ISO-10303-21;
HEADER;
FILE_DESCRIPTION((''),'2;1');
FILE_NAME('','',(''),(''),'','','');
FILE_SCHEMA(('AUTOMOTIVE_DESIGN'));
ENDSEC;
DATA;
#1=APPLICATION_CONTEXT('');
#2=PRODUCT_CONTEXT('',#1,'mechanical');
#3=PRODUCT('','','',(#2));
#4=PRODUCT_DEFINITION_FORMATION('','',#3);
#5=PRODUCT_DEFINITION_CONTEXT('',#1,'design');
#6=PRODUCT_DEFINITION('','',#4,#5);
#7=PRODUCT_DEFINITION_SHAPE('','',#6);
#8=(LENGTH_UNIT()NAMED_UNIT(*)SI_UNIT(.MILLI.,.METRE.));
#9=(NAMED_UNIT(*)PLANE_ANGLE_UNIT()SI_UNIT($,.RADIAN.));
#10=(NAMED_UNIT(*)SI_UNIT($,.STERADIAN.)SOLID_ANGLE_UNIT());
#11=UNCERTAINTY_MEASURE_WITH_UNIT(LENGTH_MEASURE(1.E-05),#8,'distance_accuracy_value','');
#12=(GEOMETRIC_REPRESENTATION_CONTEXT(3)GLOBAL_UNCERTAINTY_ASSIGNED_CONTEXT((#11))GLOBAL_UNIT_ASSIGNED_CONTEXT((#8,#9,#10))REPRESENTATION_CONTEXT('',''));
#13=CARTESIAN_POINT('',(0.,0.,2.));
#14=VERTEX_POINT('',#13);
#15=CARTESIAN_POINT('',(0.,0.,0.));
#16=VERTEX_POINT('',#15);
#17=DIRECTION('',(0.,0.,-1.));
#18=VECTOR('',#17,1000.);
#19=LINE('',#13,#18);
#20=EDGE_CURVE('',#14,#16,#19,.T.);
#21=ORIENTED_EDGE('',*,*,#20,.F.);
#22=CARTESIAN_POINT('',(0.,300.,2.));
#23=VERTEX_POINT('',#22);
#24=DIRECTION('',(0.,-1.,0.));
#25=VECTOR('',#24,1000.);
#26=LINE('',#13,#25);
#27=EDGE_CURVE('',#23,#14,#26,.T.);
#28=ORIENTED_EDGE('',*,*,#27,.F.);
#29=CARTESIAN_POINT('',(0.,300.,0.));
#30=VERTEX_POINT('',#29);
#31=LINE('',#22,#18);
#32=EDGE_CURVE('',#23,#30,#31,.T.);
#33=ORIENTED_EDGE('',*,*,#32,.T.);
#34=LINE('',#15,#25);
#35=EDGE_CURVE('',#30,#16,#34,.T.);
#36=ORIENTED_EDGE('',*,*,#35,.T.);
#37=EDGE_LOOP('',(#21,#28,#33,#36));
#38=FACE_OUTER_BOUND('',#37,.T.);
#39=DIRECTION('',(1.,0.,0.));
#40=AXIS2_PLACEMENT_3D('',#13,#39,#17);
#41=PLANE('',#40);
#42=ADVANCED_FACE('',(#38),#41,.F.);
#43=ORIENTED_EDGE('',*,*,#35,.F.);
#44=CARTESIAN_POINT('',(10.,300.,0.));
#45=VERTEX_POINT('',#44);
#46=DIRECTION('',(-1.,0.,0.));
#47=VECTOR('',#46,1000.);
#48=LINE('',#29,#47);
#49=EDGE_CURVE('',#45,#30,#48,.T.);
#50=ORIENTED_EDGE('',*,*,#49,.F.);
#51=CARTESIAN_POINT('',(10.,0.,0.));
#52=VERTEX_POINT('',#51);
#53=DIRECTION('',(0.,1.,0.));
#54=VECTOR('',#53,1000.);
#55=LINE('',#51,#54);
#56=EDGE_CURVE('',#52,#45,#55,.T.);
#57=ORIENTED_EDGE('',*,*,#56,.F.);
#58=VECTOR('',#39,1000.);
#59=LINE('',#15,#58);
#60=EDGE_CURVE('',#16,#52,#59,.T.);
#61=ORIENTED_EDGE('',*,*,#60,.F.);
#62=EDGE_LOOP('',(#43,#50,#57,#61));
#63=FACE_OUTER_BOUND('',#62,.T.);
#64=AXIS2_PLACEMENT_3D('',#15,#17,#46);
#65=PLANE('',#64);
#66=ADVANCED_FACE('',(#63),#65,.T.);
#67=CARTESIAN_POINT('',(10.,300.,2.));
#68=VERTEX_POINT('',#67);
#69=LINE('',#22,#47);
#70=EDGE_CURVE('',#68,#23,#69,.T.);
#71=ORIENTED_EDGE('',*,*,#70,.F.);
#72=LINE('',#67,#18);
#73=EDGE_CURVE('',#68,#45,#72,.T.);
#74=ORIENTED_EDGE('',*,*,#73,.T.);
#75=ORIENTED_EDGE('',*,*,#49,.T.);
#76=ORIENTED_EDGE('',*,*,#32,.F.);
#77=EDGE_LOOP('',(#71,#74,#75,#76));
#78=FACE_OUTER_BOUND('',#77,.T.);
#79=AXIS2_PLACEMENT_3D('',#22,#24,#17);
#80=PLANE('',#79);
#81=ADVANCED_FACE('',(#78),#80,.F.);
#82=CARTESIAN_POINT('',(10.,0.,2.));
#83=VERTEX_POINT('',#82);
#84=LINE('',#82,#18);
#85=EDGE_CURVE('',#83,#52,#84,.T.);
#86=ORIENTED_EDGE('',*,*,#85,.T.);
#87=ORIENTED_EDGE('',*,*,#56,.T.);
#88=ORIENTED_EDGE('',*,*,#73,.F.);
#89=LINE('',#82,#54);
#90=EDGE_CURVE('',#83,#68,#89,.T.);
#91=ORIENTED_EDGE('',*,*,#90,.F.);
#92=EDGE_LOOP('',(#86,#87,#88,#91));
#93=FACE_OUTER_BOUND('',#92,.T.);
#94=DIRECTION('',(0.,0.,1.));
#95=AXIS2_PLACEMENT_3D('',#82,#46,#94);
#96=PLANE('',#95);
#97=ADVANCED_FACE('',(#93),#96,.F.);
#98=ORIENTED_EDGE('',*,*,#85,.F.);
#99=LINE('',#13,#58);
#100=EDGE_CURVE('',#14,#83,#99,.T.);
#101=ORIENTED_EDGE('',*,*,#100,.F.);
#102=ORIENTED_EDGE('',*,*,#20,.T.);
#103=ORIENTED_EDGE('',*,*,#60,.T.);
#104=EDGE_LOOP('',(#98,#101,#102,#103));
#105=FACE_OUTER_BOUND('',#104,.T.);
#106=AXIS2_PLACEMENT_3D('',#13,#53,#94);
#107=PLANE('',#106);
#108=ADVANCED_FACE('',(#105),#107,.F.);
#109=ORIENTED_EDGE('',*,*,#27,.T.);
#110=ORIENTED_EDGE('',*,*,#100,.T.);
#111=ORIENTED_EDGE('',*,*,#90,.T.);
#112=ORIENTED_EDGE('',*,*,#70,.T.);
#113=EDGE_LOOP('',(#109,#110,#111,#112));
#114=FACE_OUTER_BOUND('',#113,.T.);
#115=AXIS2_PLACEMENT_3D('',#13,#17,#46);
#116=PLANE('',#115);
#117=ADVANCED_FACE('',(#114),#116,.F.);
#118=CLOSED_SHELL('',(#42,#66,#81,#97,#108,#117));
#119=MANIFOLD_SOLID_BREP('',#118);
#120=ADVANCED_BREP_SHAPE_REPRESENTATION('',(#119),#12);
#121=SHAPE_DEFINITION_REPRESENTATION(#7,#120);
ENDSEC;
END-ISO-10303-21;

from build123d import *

# Parameters (mm, degrees)
SKETCH1_W           = 10
SKETCH1_H           = 300
BOSS_EXTRUDE1_DEPTH = 2


with BuildPart() as part:
    # Sketch1 → Boss-Extrude1 (new body)
    with BuildSketch(Plane.XY):
        with Locations((5, 150)):
            Rectangle(SKETCH1_W, SKETCH1_H)
    extrude(amount=BOSS_EXTRUDE1_DEPTH)


solid = part.part
